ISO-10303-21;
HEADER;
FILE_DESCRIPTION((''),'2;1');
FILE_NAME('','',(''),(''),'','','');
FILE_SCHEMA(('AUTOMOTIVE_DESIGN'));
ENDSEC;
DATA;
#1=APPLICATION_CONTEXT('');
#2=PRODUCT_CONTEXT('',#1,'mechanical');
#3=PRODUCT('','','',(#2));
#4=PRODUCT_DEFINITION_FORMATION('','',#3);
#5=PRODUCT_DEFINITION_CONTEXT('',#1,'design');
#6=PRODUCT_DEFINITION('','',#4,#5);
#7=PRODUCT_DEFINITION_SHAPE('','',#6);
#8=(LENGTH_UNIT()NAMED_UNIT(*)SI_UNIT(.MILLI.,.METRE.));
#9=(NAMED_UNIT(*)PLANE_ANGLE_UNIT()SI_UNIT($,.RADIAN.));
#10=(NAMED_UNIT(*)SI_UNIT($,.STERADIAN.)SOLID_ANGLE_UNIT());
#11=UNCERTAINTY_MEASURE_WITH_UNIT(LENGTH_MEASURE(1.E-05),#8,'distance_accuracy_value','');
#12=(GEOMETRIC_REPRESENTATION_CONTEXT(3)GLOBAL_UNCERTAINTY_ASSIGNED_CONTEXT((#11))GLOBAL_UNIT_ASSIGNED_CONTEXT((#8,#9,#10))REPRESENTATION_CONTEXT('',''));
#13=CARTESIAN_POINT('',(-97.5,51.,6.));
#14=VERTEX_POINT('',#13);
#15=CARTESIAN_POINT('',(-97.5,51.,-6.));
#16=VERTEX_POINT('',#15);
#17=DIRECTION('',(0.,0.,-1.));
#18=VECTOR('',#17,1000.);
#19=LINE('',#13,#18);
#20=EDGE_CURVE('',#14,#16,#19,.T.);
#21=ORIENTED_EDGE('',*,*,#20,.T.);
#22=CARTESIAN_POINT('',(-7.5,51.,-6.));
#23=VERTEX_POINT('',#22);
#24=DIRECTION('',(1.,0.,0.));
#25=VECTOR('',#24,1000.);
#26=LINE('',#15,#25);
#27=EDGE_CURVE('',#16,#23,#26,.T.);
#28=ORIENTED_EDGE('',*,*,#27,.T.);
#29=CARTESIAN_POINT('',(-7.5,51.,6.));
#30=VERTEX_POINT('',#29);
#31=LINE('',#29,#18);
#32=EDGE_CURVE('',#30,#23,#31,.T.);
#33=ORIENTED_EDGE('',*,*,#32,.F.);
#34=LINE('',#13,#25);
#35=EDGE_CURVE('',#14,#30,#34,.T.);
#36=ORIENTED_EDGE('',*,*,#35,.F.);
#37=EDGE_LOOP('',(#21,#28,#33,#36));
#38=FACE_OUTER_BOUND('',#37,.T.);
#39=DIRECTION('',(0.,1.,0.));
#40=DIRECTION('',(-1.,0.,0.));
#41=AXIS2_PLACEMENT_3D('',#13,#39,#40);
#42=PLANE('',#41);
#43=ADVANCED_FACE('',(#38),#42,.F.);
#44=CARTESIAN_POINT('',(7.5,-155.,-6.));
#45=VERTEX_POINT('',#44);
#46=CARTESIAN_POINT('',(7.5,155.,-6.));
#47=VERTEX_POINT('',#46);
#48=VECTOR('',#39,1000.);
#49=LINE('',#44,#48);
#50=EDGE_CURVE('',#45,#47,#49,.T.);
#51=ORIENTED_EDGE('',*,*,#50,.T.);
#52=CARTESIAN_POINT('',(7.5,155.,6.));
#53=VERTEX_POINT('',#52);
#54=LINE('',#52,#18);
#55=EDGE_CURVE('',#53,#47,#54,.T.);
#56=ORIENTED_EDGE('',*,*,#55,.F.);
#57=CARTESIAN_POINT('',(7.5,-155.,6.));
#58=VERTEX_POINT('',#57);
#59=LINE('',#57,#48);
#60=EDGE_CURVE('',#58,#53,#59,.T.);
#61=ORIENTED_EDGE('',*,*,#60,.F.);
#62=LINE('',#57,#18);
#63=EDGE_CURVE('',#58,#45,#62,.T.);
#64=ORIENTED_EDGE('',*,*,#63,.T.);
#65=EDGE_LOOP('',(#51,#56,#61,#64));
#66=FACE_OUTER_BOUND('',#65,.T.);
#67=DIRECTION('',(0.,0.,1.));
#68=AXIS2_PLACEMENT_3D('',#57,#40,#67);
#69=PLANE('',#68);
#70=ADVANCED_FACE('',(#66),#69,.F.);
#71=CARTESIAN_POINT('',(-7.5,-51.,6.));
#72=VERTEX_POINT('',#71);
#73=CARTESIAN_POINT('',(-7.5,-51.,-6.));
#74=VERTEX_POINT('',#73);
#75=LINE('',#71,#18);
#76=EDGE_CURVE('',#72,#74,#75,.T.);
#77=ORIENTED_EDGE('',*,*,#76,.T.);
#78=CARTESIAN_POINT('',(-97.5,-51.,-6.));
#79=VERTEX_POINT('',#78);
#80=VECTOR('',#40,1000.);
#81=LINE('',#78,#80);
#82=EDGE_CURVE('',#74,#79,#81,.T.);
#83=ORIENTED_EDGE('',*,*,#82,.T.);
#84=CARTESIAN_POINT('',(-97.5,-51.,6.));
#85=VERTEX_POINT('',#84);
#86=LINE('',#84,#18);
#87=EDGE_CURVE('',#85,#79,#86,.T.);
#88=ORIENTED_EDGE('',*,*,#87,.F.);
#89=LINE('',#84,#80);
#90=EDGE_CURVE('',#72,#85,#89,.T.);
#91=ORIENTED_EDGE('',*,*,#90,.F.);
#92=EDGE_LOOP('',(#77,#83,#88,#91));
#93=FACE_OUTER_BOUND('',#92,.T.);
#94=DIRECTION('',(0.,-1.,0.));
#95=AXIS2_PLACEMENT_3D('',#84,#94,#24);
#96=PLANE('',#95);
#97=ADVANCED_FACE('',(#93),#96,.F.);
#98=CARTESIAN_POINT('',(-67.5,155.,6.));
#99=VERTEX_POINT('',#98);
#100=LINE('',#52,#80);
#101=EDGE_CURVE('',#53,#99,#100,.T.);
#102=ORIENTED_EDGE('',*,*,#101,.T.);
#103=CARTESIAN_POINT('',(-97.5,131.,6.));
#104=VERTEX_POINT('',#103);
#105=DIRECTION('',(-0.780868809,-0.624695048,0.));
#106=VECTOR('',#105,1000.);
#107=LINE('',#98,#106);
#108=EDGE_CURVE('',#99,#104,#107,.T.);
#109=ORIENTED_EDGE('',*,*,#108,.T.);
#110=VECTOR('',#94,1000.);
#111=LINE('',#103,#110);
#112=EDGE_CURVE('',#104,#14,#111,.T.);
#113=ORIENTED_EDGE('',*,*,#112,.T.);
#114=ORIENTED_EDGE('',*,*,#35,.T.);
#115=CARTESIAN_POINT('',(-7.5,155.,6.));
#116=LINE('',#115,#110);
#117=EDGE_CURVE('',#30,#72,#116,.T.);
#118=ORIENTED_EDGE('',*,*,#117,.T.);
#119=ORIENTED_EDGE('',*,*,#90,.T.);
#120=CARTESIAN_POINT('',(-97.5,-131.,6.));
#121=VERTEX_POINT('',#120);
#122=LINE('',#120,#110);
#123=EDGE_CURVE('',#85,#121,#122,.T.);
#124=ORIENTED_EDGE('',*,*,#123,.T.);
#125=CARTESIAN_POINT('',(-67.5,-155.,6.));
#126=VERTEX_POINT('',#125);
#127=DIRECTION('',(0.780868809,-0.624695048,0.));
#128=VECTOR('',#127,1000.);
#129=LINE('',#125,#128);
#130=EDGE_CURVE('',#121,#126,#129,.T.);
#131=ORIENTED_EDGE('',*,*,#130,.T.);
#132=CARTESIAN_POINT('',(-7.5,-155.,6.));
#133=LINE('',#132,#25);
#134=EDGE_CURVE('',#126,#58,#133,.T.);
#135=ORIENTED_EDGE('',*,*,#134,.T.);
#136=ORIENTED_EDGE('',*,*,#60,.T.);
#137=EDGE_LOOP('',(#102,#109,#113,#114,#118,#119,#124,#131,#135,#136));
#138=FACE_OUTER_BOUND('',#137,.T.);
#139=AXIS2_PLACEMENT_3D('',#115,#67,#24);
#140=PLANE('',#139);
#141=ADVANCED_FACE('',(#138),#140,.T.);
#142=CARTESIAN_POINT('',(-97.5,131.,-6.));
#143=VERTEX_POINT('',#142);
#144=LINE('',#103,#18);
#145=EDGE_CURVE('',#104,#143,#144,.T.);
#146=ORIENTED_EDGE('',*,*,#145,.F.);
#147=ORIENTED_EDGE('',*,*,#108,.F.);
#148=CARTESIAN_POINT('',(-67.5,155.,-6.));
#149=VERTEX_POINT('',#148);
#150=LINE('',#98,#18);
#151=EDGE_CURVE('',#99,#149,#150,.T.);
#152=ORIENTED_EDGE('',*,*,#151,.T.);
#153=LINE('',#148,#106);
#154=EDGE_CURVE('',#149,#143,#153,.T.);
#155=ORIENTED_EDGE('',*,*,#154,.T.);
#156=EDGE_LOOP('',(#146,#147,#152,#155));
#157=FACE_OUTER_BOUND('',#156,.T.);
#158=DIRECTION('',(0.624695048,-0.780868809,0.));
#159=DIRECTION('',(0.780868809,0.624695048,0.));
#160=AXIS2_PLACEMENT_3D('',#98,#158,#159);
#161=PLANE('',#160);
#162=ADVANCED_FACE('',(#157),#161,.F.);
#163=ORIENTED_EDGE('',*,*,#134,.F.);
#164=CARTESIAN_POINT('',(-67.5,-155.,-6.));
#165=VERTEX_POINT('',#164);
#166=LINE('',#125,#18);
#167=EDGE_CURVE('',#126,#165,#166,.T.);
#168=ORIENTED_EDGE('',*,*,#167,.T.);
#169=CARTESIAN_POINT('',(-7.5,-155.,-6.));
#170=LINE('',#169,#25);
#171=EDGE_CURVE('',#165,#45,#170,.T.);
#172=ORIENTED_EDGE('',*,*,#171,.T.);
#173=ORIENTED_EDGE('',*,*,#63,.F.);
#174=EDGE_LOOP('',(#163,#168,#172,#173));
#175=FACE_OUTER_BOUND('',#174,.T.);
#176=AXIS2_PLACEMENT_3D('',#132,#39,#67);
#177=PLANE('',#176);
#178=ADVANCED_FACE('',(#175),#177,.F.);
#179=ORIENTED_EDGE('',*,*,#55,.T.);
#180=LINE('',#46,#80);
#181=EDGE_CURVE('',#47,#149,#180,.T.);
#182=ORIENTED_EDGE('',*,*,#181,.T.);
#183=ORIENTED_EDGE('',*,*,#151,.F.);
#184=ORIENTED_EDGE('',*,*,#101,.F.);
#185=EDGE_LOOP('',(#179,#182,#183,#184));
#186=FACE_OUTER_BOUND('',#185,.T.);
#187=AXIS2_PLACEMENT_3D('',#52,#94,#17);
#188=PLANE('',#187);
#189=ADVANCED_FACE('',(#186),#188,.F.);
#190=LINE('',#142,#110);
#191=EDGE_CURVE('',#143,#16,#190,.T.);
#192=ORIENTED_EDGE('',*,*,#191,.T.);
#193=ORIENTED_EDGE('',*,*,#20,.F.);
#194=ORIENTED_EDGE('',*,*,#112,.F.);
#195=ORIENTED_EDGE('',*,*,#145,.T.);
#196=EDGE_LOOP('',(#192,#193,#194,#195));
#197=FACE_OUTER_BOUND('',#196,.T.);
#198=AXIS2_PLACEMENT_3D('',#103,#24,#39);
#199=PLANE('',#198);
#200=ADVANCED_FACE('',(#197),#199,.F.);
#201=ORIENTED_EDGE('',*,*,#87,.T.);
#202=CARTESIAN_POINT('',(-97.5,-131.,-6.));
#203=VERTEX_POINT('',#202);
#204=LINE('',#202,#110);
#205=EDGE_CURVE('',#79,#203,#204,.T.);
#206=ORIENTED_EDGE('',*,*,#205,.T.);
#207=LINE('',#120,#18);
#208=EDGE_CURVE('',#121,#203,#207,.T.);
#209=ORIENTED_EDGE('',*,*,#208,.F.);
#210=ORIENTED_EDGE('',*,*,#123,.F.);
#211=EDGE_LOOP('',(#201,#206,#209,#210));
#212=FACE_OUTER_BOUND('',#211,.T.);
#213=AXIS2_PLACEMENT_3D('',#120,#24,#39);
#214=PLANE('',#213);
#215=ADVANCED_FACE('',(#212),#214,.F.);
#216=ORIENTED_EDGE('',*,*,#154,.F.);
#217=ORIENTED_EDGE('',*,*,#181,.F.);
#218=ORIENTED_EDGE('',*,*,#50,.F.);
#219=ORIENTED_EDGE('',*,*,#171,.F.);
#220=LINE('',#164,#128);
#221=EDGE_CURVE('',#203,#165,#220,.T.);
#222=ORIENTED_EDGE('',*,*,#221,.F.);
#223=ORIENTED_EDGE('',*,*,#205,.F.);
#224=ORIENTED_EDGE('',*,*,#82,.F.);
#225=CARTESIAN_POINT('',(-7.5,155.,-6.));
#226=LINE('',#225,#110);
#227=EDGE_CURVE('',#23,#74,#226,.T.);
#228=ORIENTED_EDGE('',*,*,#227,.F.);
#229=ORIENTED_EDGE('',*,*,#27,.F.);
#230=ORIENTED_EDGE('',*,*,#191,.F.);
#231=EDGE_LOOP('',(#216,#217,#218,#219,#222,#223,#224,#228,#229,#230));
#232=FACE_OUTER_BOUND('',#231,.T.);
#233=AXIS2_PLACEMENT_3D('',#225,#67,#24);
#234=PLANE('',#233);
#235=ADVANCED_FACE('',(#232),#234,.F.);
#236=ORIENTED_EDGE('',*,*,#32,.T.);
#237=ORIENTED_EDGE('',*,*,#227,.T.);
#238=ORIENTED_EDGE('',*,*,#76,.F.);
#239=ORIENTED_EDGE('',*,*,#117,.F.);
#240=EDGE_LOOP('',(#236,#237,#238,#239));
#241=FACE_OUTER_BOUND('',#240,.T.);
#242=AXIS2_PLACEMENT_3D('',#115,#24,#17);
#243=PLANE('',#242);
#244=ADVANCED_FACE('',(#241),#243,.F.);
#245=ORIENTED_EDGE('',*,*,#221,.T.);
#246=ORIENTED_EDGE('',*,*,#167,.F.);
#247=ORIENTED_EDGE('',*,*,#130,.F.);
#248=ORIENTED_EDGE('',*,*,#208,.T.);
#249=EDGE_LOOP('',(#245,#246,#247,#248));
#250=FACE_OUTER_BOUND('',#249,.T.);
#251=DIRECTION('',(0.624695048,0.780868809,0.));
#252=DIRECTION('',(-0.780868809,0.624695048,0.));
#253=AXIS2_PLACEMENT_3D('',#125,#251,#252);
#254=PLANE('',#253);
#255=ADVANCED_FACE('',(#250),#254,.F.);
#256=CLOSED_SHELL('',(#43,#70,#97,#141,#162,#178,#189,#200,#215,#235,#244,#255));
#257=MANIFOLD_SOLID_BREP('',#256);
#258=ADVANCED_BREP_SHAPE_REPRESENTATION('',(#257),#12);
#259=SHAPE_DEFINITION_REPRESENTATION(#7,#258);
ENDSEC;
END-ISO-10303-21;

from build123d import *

# Parameters (mm, degrees)
SKETCH1_W      = 15
SKETCH1_H      = 310
EXTRUDE1_DEPTH = 6
EXTRUDE3_DEPTH = 6


with BuildPart() as part:
    # Sketch1 → Extrude1 (new, symmetric)
    with BuildSketch(Plane.XY):
        Rectangle(SKETCH1_W, SKETCH1_H)
    extrude(amount=EXTRUDE1_DEPTH, both=True)

    # Sketch3 → Extrude3 (add, symmetric)
    with BuildSketch(Plane.XY):
        Polygon((-7.5, 155), (-67.5, 155), (-97.5, 131), (-97.5, 51), (-7.5, 51), align=None)
        Polygon((-7.5, -51), (-7.5, -155), (-67.5, -155), (-97.5, -131), (-97.5, -51), align=None)
    extrude(amount=EXTRUDE3_DEPTH, both=True)


solid = part.part
